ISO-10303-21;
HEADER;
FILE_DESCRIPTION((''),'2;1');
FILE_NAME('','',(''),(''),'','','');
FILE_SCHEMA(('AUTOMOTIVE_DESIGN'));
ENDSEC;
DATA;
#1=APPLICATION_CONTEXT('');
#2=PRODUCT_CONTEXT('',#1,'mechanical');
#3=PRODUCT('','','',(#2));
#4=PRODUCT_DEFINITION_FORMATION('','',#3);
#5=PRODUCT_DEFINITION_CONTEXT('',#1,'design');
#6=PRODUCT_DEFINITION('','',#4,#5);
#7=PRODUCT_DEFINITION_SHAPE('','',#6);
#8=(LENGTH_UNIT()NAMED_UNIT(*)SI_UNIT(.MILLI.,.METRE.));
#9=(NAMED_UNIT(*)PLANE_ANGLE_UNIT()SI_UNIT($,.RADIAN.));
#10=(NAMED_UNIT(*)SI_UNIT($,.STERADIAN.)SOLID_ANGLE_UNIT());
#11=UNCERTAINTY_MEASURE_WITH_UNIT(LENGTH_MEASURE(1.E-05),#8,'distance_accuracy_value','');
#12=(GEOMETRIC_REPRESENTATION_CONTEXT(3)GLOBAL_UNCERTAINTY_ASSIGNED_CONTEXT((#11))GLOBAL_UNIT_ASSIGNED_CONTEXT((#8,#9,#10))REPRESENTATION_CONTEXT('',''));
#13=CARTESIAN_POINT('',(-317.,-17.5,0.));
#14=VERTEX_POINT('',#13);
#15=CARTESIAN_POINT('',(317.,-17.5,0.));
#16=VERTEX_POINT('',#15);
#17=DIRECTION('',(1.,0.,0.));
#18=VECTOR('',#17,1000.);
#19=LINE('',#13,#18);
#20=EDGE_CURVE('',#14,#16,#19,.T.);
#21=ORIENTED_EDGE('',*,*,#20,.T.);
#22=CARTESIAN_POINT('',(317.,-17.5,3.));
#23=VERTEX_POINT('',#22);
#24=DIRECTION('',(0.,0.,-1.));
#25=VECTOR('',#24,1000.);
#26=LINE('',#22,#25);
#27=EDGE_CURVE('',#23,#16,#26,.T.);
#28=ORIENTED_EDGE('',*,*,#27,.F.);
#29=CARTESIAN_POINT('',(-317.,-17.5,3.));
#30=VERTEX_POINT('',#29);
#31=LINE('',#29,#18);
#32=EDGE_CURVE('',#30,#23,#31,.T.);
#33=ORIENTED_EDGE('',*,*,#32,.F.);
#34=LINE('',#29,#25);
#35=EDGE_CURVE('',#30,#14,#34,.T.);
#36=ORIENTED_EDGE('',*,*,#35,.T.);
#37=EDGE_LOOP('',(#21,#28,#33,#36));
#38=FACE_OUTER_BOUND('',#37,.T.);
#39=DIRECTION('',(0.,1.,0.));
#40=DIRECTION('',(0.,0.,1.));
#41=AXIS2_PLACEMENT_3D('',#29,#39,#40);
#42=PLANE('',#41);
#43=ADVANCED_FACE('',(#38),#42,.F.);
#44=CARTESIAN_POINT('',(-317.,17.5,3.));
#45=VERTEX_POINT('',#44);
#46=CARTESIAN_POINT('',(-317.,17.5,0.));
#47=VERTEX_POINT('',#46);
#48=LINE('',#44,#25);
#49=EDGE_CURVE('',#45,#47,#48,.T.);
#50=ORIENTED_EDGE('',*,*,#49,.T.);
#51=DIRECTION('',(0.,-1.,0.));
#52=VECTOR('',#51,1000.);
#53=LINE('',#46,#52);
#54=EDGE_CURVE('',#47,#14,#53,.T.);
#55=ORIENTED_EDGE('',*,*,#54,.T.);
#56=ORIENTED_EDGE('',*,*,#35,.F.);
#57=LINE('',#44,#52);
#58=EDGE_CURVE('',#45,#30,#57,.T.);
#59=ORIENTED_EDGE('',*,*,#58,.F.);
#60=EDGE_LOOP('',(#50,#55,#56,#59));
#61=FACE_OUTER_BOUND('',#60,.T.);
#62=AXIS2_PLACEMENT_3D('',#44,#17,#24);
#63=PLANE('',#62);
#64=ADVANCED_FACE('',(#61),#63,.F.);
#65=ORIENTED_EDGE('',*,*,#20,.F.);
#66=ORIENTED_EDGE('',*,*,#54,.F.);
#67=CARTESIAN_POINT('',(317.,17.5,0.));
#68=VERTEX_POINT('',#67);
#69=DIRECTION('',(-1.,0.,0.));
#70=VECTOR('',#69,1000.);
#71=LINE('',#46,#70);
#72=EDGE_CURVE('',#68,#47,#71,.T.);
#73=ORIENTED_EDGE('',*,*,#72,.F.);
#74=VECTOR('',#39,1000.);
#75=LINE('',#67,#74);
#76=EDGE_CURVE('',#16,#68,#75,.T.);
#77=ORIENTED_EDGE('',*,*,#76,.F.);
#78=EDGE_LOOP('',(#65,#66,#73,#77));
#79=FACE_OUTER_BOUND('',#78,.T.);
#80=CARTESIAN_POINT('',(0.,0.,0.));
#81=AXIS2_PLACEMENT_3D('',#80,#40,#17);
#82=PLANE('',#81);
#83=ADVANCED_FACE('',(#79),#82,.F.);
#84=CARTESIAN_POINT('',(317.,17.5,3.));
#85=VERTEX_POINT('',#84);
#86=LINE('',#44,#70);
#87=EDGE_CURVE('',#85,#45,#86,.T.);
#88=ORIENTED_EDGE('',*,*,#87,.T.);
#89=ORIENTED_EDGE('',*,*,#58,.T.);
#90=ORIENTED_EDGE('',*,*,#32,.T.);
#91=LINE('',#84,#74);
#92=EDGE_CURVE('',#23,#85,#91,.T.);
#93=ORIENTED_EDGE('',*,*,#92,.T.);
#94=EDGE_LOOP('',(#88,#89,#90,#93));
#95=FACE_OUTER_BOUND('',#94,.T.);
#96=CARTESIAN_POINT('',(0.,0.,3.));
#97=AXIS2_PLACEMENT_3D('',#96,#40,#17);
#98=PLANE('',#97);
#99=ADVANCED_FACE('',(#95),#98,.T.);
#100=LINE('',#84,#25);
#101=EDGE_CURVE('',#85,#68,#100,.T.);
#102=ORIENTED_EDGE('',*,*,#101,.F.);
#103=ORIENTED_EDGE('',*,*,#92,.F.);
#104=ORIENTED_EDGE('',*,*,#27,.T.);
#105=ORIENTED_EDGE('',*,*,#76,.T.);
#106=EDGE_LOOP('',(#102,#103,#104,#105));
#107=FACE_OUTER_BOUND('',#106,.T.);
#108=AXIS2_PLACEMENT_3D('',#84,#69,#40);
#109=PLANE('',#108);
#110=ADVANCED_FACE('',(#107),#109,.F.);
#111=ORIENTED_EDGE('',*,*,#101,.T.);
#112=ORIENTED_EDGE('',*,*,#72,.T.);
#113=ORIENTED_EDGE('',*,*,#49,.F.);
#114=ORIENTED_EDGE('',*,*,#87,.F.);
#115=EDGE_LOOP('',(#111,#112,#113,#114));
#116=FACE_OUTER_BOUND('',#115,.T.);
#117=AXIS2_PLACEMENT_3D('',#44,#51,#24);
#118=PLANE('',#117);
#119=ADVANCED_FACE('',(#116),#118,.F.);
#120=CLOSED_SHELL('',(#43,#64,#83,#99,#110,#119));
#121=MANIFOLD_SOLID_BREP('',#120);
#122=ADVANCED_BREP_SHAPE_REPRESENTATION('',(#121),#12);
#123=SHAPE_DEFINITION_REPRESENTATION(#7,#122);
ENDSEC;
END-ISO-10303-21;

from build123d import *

# Parameters (mm, degrees)
SKETCH_1_W      = 634
SKETCH_1_H      = 35
EXTRUDE_1_DEPTH = 3


with BuildPart() as part:
    # 草图1 → 凸台-拉伸1 (new body)
    with BuildSketch(Plane.XY):
        Rectangle(SKETCH_1_W, SKETCH_1_H)
    extrude(amount=EXTRUDE_1_DEPTH)


solid = part.part
